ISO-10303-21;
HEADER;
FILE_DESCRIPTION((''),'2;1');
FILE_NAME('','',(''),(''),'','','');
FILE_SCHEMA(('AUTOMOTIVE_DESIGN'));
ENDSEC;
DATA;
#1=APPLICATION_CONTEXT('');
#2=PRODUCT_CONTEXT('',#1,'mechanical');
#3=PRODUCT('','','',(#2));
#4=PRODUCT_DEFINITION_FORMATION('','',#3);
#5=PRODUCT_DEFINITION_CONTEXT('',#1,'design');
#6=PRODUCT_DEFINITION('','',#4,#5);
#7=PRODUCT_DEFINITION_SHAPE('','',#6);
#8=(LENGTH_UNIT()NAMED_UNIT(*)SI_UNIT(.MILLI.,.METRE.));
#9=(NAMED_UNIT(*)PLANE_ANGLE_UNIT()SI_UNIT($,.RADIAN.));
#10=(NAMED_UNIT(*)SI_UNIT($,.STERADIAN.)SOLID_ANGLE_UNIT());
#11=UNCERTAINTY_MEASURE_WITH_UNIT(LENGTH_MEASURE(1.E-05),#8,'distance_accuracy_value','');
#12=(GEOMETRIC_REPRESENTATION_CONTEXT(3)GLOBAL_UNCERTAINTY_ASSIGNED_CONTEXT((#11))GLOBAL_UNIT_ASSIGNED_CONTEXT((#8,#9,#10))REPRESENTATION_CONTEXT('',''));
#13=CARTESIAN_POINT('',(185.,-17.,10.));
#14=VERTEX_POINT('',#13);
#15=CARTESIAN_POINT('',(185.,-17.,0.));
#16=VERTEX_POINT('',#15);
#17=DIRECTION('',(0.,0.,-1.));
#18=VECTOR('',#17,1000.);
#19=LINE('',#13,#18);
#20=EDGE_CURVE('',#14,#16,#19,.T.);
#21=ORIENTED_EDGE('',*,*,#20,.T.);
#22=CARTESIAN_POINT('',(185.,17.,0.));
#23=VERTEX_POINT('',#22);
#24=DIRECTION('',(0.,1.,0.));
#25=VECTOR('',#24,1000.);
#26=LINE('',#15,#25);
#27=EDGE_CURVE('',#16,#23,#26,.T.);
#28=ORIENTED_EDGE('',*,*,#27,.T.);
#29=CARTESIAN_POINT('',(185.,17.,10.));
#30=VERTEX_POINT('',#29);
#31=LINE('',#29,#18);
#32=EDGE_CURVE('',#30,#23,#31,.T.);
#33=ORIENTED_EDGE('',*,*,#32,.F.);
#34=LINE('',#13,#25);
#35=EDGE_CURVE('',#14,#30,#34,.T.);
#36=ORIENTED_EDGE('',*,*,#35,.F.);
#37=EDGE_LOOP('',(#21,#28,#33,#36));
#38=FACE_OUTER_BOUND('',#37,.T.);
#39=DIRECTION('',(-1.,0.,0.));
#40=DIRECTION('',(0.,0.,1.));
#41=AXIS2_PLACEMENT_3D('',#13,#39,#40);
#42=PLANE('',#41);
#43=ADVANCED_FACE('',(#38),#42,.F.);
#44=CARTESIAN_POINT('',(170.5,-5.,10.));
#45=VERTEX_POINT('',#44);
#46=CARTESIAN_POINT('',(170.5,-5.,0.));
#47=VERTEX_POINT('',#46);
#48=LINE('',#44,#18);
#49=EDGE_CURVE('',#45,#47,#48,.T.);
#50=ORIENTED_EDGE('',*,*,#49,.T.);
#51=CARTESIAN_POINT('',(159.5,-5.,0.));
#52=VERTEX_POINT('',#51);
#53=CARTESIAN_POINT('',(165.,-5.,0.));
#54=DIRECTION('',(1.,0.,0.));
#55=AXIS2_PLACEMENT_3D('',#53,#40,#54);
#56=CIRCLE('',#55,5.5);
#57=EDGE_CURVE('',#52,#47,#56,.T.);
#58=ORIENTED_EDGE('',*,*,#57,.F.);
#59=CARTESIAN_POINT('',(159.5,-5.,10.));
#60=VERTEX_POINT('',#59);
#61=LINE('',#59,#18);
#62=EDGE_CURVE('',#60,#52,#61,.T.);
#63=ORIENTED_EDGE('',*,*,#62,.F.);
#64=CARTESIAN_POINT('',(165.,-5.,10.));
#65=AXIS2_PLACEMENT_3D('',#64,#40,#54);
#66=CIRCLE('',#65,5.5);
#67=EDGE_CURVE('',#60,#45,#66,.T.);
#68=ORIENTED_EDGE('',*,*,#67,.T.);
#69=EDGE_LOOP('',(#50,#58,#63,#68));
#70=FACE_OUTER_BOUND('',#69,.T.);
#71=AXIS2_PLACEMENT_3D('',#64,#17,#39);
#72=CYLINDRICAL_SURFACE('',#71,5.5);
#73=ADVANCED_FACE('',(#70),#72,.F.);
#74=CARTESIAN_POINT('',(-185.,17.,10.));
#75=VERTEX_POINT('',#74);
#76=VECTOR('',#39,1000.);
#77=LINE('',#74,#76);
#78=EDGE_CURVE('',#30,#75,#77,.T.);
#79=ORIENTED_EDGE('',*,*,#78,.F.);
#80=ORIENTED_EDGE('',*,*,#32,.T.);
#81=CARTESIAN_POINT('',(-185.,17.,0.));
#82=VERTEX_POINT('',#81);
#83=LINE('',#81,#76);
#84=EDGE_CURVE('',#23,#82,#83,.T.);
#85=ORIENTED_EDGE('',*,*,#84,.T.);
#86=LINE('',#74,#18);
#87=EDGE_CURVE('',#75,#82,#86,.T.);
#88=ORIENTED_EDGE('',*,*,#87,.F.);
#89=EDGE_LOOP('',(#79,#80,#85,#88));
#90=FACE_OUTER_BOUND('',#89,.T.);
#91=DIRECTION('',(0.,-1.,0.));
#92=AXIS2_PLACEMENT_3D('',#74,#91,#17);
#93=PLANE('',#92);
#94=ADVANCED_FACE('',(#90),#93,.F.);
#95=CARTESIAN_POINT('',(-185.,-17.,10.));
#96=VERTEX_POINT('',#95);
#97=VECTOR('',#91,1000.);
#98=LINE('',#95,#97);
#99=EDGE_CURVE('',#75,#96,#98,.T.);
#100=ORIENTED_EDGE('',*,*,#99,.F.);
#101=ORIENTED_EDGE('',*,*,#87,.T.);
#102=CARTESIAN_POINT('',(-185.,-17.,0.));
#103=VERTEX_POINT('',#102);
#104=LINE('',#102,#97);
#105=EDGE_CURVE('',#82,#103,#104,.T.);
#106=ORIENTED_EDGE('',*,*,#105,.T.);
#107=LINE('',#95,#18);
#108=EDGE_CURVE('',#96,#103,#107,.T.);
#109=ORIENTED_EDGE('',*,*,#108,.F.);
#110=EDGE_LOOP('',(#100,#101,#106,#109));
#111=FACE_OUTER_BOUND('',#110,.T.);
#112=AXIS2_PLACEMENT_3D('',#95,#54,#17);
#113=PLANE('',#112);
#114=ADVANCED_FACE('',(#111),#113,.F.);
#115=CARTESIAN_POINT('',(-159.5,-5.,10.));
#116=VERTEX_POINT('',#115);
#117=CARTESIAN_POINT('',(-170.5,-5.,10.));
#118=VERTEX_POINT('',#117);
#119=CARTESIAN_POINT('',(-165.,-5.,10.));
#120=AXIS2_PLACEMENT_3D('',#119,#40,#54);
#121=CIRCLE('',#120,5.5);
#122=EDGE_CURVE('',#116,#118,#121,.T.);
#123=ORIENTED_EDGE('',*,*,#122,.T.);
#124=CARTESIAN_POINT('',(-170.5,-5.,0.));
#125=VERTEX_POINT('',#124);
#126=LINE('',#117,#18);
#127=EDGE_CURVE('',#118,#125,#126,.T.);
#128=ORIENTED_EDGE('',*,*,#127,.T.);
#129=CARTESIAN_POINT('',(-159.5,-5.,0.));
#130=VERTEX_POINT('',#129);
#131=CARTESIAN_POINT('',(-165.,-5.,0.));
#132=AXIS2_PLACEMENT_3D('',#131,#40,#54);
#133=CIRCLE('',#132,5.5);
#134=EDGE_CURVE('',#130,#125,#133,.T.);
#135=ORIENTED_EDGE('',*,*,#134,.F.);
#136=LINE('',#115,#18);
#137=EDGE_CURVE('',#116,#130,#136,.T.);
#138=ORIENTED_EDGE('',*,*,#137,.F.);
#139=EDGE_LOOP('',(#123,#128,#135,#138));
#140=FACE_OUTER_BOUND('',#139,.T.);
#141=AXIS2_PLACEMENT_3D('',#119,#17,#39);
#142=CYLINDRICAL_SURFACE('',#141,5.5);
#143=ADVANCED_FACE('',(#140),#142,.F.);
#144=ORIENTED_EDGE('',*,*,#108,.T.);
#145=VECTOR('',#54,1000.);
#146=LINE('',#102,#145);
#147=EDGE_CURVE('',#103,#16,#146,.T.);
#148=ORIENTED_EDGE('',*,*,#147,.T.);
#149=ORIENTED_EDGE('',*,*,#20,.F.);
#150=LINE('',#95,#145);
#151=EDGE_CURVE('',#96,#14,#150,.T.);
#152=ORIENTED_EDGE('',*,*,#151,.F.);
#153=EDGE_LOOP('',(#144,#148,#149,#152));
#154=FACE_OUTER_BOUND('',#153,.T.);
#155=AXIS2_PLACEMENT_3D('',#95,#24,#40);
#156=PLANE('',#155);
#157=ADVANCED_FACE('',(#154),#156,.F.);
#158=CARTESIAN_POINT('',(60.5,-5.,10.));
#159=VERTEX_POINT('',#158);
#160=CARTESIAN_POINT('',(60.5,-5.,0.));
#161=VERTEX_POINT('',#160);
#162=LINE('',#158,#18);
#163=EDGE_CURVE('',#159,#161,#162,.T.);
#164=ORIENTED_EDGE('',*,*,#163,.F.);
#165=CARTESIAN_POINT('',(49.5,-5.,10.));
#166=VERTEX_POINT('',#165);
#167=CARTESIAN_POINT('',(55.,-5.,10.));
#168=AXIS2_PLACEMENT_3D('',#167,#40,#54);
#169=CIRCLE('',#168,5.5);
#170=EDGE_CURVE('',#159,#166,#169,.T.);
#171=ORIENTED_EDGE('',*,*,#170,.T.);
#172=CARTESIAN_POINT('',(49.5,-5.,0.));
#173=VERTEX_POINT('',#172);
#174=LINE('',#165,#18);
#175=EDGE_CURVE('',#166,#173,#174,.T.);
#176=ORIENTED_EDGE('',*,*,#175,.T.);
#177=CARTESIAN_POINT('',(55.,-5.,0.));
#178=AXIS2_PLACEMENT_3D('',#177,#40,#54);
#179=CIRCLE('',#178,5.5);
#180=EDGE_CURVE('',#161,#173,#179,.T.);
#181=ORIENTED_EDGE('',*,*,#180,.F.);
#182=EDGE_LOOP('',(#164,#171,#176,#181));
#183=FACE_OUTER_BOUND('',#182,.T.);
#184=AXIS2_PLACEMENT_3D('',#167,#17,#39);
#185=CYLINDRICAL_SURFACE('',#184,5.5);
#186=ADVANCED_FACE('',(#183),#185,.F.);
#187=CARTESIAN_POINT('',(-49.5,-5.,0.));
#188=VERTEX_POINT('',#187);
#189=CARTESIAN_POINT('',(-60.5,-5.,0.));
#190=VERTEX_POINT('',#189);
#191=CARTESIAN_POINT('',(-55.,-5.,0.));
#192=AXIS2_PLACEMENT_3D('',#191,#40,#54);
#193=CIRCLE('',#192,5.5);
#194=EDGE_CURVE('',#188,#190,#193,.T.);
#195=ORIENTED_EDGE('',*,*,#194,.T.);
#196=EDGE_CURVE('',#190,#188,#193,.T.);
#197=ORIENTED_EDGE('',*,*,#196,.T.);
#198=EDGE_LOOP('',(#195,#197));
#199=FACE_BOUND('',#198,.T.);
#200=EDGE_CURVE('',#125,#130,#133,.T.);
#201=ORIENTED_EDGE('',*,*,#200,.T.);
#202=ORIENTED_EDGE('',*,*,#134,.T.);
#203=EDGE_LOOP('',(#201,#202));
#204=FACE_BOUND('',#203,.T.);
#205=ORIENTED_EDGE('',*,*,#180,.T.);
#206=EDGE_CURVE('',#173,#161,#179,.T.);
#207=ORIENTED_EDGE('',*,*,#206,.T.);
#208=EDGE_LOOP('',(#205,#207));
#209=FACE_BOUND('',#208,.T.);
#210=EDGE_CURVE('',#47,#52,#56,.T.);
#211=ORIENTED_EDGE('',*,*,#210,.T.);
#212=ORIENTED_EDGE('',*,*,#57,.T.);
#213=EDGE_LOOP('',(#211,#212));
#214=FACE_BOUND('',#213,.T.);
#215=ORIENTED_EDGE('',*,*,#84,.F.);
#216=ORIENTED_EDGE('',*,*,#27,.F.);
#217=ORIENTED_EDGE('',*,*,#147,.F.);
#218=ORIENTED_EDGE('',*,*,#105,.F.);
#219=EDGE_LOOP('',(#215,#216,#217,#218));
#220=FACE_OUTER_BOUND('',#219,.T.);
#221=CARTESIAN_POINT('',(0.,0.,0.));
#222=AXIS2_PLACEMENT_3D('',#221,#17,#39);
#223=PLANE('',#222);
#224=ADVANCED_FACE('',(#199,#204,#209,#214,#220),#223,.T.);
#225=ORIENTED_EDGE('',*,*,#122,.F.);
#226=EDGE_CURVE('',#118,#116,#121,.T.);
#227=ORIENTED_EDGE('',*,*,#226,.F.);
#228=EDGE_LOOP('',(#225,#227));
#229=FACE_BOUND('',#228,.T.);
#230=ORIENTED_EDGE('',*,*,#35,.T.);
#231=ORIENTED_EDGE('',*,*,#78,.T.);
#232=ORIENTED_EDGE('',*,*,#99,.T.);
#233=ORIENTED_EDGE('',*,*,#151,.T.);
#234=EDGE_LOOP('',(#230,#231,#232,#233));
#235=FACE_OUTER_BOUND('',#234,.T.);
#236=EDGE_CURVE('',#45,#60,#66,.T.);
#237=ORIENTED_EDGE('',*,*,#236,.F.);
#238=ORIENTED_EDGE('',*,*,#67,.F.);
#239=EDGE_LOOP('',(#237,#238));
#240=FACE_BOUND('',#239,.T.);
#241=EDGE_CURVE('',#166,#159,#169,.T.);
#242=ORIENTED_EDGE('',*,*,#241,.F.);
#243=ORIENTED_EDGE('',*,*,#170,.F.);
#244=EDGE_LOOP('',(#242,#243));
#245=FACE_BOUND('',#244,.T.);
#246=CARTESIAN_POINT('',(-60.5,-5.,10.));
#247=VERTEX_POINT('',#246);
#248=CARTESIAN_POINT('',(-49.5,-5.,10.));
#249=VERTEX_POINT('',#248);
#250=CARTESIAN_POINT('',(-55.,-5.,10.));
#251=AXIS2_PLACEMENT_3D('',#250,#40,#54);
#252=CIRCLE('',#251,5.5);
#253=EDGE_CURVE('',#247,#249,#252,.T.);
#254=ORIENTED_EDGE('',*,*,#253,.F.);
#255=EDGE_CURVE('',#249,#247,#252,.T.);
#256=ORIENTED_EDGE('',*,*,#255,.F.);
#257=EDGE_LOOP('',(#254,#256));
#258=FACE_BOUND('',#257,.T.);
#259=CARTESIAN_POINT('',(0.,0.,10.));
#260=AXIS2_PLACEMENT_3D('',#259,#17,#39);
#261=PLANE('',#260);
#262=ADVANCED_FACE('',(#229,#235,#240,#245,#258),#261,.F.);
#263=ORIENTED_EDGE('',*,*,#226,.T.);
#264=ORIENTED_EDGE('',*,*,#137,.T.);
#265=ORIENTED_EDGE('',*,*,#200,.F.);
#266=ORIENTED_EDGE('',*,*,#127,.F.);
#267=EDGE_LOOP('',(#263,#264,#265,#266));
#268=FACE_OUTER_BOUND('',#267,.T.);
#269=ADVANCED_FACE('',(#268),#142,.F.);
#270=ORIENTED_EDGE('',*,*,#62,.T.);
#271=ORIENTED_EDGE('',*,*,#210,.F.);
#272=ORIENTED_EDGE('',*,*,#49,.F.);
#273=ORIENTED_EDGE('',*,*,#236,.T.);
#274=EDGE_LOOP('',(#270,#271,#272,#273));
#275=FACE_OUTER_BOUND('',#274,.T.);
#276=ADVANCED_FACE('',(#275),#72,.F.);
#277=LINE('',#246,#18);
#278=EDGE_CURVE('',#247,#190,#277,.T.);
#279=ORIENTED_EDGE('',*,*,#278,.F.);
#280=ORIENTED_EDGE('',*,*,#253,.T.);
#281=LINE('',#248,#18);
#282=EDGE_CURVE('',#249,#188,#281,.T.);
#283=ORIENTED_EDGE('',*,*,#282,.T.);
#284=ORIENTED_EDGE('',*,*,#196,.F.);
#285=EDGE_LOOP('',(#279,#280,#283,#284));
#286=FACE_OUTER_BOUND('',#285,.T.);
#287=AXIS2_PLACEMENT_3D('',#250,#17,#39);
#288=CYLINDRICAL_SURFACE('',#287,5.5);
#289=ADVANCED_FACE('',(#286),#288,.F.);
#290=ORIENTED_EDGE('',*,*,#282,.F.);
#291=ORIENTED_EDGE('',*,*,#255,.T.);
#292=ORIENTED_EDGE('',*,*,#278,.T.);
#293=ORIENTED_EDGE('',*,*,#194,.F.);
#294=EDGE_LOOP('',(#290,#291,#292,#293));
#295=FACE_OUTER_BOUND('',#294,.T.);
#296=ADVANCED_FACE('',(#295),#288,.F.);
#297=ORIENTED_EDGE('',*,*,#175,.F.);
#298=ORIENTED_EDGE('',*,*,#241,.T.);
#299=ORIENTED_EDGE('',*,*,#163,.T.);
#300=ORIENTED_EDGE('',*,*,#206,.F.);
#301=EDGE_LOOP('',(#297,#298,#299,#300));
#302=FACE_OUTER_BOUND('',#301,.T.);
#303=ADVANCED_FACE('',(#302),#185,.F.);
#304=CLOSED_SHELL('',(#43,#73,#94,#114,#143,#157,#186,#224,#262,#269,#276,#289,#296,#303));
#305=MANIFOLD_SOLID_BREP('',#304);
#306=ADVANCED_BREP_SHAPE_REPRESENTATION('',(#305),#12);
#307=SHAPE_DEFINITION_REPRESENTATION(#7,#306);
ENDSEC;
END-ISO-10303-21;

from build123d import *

# Parameters (mm, degrees)
SKETCH_1_W      = 370
SKETCH_1_H      = 34
SKETCH_1_R      = 5.5
EXTRUDE_1_DEPTH = 10


with BuildPart() as part:
    # 草图1 → 凸台-拉伸1 (new body)
    with BuildSketch(Plane.XY):
        Rectangle(SKETCH_1_W, SKETCH_1_H)
        with Locations((165, -5)):
            Circle(SKETCH_1_R, mode=Mode.SUBTRACT)
        with Locations((55, -5)):
            Circle(SKETCH_1_R, mode=Mode.SUBTRACT)
        with Locations((-55, -5)):
            Circle(SKETCH_1_R, mode=Mode.SUBTRACT)
        with Locations((-165, -5)):
            Circle(SKETCH_1_R, mode=Mode.SUBTRACT)
    extrude(amount=EXTRUDE_1_DEPTH)


solid = part.part
